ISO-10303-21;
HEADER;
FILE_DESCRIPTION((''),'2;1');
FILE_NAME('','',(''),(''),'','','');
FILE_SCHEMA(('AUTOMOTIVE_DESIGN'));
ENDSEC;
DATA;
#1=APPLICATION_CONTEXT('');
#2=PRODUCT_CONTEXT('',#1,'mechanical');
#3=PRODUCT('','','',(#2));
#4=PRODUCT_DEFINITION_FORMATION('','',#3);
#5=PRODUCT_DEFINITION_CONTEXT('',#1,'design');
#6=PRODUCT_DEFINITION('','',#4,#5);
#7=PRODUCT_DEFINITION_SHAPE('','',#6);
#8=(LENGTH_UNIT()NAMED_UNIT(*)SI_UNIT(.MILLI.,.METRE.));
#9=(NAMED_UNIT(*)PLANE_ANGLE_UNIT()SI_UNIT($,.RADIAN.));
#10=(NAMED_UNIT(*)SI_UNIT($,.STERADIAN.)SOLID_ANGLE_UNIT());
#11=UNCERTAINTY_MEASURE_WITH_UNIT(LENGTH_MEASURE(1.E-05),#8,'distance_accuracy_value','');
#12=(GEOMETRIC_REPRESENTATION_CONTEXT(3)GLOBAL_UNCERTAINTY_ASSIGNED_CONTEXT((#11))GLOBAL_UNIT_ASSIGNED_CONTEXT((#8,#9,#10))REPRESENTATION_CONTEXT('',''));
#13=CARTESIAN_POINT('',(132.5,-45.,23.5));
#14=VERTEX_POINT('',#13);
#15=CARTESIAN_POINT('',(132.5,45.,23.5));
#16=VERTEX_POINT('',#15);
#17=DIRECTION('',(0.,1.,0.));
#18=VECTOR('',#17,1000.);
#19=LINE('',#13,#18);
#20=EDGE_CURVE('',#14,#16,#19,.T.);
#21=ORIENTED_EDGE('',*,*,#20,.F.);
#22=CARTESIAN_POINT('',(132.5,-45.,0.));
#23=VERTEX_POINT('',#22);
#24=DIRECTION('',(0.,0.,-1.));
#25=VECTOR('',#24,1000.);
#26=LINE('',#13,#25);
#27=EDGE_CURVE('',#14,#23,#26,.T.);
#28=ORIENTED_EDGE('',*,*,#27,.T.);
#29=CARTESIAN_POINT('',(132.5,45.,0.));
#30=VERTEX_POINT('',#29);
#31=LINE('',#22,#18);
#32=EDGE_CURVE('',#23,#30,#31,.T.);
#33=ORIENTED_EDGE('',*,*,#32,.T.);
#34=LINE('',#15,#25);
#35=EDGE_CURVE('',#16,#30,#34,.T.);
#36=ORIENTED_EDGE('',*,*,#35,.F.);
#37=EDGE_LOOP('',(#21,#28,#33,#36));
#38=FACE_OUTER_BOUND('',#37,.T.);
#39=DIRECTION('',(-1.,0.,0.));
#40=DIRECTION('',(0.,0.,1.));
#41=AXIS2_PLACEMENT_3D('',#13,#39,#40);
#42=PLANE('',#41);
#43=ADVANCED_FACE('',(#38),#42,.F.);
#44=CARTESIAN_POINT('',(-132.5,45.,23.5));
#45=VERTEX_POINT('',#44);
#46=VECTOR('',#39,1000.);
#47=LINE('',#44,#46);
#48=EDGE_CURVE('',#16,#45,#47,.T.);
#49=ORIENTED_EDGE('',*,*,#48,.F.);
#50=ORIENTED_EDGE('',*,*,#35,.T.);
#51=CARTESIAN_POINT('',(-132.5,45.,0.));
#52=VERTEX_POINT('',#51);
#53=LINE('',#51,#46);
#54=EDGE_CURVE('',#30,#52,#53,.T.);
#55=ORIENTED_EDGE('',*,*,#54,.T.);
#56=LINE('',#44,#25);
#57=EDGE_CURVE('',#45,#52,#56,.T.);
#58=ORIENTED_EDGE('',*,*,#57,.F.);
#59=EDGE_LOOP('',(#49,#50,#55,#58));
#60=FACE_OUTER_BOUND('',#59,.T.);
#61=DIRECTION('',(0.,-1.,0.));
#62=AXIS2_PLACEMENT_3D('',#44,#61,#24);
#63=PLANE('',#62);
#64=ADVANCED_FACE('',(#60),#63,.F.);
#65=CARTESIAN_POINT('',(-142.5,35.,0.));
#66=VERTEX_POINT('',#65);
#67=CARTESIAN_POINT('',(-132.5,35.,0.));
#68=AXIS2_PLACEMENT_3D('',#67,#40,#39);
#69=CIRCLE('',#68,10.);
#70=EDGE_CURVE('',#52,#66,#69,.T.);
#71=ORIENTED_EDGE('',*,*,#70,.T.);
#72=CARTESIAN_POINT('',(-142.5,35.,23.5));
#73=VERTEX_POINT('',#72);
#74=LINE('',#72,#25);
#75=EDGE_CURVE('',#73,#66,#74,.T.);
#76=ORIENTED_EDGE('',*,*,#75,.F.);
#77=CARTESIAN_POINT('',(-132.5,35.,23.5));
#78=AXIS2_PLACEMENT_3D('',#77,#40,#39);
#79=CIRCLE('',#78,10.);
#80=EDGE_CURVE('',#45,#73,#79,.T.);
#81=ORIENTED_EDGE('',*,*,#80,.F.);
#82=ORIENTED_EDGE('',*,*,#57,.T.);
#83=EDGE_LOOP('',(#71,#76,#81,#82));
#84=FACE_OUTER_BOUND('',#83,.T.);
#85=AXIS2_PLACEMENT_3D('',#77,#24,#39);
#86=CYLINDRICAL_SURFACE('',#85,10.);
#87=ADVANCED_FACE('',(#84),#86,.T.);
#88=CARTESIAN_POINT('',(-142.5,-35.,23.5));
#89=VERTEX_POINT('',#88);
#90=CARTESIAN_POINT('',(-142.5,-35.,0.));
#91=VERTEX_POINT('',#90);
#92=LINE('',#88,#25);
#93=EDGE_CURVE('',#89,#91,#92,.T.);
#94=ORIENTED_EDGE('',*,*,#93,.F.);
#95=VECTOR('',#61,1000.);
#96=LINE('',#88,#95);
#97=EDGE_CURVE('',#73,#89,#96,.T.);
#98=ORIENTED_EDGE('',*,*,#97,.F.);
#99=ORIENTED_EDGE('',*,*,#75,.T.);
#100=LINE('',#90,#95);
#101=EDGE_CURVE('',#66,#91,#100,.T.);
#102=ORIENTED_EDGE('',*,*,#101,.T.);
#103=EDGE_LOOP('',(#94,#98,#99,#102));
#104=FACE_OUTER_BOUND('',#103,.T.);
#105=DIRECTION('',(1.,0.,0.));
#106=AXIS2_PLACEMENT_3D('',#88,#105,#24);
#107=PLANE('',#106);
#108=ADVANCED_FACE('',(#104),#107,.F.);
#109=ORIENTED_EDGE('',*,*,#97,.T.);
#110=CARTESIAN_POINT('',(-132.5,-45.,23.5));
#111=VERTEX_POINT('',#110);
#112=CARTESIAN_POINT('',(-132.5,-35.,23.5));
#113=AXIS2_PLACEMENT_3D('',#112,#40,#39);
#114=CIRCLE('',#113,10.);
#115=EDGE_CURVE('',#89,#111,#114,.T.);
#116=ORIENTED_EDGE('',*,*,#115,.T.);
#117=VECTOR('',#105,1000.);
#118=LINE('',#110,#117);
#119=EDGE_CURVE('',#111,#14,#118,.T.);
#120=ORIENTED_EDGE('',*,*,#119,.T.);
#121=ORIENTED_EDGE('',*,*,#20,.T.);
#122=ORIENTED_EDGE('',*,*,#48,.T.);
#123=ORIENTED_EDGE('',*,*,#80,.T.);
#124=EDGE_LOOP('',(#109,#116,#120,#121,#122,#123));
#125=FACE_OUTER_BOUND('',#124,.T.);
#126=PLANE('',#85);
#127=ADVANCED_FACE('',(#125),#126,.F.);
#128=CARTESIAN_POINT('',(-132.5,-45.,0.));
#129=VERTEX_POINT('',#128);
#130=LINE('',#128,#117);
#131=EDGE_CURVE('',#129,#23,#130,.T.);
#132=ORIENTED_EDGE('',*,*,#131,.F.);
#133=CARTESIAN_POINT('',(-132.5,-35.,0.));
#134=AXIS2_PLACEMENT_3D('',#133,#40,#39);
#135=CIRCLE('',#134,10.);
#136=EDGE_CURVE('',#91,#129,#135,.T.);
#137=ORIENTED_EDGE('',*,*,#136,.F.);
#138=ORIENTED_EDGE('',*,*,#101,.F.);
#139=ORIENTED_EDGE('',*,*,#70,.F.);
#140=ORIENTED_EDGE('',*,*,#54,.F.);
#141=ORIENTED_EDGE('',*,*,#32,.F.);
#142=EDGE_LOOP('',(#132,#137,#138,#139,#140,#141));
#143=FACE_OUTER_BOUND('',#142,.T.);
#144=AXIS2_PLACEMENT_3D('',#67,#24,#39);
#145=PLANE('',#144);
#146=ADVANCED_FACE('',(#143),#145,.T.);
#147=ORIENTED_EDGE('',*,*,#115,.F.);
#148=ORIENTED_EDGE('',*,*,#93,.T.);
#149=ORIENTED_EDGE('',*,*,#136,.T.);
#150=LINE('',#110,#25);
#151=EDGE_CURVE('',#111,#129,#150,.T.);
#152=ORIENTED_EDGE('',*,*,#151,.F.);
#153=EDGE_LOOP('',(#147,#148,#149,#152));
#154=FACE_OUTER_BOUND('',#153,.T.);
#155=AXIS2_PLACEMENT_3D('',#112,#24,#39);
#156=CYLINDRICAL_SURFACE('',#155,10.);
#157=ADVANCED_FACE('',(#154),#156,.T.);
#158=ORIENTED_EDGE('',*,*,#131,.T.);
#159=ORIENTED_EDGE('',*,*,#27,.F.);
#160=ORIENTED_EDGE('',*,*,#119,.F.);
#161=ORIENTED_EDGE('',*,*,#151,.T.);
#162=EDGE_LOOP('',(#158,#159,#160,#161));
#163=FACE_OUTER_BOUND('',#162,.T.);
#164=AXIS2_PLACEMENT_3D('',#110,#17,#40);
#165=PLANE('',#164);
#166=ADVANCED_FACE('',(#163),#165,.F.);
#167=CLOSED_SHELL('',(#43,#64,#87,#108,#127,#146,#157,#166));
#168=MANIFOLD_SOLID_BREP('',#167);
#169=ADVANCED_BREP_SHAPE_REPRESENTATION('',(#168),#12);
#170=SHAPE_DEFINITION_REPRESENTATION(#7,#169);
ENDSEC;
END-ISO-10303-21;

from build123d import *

# Parameters (mm, degrees)
EXTRUDE_1_DEPTH = 23.5


with BuildPart() as part:
    # 草图1 → 凸台-拉伸1 (new body)
    with BuildSketch(Plane.XY):
        with BuildLine():
            Line((-132.5, -45), (132.5, -45))
            Line((132.5, -45), (132.5, 45))
            Line((132.5, 45), (-132.5, 45))
            ThreePointArc((-132.5, 45), (-139.571067812, 42.071067812), (-142.5, 35))
            Line((-142.5, 35), (-142.5, -35))
            ThreePointArc((-142.5, -35), (-139.571067812, -42.071067812), (-132.5, -45))
        make_face()
    extrude(amount=EXTRUDE_1_DEPTH)


solid = part.part
